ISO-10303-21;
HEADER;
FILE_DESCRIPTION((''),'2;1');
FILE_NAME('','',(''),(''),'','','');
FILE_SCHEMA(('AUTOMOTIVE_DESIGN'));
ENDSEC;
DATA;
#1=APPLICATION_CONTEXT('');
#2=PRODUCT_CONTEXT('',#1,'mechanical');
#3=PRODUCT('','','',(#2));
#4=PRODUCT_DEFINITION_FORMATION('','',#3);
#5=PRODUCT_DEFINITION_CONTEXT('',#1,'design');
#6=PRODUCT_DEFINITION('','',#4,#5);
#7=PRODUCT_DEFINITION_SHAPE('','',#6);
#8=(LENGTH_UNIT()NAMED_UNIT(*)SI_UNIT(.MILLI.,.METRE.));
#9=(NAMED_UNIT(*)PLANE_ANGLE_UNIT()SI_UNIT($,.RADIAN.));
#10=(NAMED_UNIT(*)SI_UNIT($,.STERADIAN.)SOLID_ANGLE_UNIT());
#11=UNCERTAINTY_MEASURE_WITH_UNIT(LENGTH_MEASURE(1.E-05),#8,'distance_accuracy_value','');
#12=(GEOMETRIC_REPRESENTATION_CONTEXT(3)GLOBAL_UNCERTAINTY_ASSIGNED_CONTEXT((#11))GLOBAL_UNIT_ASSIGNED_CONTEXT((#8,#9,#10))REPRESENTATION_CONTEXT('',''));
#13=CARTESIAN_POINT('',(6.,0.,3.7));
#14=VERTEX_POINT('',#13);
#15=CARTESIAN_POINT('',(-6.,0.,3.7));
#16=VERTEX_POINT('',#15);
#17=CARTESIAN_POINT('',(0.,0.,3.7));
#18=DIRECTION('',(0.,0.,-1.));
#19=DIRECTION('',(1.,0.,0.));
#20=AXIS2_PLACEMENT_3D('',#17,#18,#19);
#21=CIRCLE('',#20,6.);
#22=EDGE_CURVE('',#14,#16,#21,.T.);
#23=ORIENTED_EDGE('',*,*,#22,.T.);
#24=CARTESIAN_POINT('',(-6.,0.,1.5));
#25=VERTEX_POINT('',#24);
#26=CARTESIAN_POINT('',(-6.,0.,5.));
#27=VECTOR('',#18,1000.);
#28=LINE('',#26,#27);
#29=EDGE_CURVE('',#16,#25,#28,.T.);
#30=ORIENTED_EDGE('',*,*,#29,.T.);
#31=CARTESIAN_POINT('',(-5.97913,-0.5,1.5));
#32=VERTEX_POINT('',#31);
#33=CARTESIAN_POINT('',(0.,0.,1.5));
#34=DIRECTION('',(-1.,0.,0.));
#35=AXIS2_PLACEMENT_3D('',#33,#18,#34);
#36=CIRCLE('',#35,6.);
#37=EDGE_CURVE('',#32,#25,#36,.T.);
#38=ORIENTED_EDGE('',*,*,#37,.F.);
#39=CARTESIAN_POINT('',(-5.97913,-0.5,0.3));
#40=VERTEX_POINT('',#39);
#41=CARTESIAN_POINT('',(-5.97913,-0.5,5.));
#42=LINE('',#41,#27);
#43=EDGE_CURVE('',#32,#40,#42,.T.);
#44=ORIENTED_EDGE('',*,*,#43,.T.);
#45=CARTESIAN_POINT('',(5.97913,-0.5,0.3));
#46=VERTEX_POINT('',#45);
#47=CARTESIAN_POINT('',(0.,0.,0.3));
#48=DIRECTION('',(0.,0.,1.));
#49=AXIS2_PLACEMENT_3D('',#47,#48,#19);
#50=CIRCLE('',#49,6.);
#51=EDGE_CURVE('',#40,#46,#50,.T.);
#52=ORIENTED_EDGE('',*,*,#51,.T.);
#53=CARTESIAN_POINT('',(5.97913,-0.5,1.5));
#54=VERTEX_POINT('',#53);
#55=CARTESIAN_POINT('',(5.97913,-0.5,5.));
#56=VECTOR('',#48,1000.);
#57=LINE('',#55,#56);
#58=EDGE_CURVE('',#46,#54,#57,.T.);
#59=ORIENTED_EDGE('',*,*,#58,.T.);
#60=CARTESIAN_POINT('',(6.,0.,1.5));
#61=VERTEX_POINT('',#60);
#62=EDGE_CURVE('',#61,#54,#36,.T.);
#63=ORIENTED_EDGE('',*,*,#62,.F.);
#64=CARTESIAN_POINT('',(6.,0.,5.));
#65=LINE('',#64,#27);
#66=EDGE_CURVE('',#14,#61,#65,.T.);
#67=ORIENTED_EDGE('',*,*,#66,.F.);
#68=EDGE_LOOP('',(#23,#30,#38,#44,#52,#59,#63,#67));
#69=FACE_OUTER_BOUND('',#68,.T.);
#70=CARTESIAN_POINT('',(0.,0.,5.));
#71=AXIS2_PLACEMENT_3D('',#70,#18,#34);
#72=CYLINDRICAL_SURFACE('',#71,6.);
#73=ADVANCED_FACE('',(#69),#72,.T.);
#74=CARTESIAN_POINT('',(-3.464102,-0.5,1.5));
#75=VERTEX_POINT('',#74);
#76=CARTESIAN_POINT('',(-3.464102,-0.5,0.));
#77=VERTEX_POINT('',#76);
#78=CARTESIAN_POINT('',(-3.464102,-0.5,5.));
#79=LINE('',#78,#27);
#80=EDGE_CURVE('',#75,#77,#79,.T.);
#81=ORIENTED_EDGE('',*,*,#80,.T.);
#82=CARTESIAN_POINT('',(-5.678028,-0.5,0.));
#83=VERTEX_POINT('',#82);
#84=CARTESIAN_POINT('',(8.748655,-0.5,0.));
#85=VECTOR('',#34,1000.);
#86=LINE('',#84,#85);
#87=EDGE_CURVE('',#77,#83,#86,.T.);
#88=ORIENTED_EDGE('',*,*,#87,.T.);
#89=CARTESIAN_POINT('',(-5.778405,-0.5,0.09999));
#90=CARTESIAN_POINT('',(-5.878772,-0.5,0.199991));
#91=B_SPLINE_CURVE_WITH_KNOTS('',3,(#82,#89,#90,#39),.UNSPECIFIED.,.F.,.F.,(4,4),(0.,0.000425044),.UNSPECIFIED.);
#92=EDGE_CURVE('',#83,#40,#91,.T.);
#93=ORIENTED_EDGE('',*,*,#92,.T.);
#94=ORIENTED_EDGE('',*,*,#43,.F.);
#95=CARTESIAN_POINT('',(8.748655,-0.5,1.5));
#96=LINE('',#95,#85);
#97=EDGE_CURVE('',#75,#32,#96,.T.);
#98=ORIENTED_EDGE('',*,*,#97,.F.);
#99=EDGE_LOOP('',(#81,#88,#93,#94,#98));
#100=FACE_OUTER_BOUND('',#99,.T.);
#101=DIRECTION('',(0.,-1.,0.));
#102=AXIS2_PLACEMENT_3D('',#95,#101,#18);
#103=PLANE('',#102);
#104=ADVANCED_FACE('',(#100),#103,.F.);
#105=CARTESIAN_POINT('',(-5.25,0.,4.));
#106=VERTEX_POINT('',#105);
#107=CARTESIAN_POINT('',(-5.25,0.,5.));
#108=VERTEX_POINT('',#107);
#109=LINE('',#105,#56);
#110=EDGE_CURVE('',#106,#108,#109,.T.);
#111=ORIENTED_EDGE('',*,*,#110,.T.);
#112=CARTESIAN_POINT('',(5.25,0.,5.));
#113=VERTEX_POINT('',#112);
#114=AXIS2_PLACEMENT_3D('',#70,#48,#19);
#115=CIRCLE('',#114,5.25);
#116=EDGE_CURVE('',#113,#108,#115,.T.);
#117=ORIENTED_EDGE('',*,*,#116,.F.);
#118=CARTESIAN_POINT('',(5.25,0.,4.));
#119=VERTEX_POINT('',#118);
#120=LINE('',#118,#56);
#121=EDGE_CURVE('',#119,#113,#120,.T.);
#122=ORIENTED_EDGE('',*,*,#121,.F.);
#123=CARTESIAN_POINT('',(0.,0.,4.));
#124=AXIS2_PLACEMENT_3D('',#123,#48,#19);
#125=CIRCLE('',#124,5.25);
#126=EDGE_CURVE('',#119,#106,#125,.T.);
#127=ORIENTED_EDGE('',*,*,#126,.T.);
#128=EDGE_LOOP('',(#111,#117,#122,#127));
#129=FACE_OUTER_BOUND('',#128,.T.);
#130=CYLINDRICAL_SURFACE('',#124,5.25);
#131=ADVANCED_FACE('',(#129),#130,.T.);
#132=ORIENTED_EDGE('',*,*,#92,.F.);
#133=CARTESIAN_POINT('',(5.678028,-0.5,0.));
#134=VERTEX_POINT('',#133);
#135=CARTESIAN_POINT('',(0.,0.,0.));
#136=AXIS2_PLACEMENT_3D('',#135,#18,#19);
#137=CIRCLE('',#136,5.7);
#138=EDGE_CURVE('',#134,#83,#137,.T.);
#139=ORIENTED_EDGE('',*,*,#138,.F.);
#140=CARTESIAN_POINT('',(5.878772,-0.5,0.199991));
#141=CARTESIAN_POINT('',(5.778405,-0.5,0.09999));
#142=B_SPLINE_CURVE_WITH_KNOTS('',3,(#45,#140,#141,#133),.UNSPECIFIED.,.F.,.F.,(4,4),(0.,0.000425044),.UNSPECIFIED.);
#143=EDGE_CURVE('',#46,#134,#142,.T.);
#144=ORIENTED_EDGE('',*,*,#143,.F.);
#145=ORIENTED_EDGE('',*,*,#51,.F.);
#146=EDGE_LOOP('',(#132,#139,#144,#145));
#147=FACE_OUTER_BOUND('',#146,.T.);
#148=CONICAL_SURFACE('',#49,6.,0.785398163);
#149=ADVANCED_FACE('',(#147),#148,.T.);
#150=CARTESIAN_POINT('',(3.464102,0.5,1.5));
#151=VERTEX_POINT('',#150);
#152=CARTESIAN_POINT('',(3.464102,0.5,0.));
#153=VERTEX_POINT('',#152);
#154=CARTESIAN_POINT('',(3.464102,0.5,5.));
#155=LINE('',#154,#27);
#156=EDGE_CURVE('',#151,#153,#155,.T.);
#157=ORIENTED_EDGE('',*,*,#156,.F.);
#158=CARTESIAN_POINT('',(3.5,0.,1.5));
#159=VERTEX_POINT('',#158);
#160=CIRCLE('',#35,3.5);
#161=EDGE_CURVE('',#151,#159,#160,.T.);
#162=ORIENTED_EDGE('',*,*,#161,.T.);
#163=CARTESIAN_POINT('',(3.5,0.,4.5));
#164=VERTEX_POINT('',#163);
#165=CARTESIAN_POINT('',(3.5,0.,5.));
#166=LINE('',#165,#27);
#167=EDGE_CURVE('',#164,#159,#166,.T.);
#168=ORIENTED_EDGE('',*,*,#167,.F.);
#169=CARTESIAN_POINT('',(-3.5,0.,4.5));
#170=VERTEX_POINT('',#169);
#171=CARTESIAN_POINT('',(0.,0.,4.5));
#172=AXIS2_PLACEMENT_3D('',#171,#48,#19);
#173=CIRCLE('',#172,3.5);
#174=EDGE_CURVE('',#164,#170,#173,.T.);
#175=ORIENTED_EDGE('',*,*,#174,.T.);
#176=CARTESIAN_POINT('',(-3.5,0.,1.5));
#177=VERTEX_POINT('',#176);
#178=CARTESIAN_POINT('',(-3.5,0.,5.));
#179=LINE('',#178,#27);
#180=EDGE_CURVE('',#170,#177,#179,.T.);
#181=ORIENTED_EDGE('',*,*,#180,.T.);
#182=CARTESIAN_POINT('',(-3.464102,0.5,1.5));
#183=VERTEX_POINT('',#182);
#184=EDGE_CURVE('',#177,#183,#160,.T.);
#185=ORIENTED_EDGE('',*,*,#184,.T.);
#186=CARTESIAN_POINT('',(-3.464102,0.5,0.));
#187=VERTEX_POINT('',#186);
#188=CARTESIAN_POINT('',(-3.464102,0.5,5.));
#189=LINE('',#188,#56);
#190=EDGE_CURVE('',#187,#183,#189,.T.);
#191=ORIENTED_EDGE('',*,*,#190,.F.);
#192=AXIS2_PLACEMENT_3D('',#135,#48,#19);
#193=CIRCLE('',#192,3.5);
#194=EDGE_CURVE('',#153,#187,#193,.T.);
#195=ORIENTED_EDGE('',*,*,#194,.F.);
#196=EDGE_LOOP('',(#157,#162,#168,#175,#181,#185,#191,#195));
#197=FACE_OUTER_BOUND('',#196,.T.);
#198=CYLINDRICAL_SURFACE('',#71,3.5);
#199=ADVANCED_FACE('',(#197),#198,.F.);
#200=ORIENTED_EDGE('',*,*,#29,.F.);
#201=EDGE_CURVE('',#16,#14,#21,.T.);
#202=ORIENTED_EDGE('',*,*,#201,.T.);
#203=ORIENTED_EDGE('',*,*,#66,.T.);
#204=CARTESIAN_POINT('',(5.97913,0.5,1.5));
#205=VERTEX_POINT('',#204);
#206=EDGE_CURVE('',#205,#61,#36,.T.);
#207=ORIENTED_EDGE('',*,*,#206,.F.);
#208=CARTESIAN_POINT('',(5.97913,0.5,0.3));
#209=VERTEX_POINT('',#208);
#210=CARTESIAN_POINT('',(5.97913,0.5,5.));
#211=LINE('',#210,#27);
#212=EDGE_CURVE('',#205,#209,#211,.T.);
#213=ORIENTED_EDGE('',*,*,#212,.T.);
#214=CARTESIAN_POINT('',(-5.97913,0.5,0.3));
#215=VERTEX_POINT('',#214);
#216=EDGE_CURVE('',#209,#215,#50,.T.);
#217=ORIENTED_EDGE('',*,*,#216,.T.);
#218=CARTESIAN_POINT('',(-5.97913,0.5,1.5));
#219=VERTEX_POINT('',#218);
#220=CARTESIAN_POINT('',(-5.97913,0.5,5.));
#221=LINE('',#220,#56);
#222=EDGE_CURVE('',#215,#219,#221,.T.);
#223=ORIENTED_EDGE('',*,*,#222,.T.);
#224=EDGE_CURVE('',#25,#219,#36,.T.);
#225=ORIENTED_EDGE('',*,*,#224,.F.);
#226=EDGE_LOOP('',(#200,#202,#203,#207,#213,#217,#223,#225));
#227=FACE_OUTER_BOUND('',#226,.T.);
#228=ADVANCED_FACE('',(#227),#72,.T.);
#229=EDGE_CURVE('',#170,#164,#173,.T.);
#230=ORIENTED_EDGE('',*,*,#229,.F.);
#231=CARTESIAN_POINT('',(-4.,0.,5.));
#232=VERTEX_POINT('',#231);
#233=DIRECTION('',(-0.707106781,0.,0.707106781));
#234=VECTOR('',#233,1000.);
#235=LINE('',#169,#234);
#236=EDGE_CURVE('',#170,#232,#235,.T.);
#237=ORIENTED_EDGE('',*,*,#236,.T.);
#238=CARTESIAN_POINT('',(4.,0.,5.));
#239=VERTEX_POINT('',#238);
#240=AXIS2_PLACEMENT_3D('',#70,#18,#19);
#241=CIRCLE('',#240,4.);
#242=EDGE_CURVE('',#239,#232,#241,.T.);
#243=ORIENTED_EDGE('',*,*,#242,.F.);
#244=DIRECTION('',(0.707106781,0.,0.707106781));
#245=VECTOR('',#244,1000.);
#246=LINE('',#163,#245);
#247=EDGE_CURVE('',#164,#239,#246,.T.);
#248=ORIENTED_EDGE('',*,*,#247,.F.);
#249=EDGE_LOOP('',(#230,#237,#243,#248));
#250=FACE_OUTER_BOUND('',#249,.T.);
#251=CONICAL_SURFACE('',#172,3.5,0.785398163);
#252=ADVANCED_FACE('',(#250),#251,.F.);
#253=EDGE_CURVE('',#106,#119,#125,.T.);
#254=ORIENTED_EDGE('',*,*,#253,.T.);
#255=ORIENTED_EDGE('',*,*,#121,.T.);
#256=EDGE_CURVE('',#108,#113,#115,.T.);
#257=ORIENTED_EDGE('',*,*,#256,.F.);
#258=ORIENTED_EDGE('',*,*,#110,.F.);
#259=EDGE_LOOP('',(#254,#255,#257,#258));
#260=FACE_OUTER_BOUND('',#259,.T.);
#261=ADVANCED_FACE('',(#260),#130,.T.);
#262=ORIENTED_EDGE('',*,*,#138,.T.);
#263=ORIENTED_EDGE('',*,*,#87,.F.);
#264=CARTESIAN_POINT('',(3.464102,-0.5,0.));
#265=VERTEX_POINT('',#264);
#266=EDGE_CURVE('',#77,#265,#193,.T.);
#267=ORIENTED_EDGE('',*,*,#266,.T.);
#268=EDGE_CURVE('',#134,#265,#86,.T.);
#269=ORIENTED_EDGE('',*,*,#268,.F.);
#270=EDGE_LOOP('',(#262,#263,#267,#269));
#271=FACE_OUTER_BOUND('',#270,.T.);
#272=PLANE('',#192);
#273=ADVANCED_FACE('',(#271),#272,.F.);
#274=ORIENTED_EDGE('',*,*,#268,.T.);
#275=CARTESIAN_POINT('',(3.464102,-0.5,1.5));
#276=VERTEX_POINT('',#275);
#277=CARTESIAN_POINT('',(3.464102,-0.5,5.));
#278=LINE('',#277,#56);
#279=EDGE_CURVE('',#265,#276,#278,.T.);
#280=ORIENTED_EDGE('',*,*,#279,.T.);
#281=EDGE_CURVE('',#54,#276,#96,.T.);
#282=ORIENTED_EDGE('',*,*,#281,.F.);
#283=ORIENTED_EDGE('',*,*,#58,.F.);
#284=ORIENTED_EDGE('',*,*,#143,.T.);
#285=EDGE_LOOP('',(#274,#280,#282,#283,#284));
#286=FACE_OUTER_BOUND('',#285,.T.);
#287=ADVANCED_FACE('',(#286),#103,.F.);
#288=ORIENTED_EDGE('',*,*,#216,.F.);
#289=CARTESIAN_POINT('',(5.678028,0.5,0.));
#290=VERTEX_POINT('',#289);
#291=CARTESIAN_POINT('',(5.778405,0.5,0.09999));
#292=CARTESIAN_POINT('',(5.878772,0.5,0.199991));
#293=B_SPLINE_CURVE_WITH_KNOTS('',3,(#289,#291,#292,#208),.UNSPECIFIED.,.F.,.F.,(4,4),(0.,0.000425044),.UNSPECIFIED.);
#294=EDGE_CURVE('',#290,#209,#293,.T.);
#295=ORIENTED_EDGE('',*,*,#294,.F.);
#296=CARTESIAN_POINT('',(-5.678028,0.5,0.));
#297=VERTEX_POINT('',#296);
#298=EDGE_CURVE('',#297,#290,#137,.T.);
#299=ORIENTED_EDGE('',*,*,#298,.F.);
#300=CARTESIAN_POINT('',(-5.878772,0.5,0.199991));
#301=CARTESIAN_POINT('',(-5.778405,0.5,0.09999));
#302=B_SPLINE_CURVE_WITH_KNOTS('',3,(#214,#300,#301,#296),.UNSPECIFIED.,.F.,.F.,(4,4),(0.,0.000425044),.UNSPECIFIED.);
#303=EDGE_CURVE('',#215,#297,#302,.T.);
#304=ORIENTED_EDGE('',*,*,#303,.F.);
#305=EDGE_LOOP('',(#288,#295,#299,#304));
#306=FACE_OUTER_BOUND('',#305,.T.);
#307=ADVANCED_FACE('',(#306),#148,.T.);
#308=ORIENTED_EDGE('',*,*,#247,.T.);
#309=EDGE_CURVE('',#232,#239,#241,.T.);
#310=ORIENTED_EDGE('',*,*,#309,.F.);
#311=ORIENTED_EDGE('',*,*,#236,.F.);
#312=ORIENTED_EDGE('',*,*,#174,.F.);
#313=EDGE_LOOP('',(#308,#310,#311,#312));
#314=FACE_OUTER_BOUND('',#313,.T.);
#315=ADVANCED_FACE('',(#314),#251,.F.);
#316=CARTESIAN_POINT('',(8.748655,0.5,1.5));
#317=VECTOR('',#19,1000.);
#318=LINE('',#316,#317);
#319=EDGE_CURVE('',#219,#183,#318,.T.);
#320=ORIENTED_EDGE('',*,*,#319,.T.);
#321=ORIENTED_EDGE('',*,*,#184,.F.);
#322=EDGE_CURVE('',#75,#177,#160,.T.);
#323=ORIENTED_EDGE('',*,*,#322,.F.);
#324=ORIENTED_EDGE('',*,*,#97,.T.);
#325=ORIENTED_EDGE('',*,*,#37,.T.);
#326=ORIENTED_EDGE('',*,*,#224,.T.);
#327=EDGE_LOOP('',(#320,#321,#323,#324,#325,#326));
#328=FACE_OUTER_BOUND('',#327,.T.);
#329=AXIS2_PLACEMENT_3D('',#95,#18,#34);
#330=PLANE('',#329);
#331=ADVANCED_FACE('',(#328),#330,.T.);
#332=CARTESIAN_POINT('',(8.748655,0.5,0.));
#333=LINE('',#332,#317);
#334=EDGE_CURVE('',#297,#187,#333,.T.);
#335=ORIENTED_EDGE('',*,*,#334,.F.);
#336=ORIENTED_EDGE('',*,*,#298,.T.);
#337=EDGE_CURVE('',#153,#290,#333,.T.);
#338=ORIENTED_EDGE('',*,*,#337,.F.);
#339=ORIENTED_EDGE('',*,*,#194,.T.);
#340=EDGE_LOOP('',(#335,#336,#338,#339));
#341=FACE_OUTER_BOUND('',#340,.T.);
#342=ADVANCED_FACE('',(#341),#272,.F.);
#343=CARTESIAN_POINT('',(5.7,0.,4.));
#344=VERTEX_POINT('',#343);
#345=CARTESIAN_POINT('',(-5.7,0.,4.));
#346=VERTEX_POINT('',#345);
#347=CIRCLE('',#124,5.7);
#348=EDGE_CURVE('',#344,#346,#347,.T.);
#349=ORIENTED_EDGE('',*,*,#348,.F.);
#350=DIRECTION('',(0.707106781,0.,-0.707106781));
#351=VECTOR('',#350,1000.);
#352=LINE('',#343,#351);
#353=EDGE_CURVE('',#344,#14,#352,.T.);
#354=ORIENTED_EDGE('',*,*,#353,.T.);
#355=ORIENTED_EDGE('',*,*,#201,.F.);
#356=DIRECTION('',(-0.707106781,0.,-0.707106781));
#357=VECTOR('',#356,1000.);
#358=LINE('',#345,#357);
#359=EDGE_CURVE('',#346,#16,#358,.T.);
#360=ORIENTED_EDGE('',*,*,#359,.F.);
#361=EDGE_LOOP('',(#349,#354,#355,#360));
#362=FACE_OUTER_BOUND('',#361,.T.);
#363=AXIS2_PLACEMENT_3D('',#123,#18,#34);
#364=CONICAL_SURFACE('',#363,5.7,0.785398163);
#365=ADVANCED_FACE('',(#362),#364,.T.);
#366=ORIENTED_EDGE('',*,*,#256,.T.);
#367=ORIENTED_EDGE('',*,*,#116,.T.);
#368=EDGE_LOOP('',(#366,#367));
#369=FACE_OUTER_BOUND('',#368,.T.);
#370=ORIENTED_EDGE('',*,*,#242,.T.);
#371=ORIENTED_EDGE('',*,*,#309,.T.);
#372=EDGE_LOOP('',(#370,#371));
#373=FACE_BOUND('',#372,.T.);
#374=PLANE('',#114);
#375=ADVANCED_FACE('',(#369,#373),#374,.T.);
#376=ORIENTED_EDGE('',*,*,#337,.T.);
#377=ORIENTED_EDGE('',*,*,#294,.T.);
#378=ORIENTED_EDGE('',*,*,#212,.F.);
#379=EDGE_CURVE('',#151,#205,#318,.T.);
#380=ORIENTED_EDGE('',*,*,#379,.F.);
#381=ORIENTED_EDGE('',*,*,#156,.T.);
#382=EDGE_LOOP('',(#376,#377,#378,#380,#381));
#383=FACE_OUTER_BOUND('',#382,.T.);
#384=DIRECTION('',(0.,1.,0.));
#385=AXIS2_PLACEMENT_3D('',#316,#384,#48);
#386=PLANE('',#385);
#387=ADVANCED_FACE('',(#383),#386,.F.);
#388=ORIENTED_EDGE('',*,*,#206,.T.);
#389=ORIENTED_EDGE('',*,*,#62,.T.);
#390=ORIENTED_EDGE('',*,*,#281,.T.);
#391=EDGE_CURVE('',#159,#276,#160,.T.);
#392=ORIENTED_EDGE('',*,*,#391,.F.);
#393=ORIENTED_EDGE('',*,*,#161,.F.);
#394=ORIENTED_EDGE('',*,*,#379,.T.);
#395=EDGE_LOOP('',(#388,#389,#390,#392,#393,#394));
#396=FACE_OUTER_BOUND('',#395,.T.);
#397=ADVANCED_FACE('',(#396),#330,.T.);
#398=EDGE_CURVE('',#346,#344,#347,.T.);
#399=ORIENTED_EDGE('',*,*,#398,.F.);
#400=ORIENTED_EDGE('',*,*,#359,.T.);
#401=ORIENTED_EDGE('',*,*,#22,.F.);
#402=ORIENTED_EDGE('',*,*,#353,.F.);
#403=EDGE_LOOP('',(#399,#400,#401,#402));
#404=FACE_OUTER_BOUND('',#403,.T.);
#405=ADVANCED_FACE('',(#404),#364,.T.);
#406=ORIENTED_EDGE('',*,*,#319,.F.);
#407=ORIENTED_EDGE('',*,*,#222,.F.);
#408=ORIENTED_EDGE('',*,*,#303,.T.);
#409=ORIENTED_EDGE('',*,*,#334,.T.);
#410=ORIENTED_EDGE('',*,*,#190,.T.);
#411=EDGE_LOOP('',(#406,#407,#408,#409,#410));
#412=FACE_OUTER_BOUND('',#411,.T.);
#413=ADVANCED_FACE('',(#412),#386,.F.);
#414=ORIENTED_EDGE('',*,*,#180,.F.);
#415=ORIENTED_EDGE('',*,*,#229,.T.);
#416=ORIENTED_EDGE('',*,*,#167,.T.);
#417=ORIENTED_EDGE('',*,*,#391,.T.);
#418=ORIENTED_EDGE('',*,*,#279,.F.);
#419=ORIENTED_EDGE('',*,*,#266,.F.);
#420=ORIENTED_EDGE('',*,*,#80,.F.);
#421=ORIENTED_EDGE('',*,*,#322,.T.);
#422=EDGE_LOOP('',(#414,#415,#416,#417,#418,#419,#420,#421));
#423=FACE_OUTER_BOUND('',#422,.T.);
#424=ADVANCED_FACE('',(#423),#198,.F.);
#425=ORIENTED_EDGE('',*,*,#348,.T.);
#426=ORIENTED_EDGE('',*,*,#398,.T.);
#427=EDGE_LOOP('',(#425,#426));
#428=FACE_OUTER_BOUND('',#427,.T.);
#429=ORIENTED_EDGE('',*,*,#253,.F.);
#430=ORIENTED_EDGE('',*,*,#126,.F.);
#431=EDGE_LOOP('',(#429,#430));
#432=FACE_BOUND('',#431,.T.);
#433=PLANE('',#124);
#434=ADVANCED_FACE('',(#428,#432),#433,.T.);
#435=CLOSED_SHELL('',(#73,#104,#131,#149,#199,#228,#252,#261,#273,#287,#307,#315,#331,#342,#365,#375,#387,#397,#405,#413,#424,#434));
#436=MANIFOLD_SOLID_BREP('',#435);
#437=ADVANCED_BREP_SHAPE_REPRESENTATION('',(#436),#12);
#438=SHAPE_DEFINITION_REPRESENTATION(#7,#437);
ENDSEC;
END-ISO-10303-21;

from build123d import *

# Parameters (mm, degrees)
SKETCH_1_R          = 6
SKETCH_1_R_2        = 3.5
EXTRUDE_1_DEPTH     = 5
CHAMFER_1_SIZE      = 0.5
SKETCH_2_W          = 16.841160442
SKETCH_2_H          = 1
CUT_EXTRUDE_1_DEPTH = 1.5
CUT_EXTRUDE_START   = -1
SKETCH_3_R          = 6
SKETCH_3_R_2        = 5.25
CUT_EXTRUDE_2_DEPTH = 1
CHAMFER_2_SIZE      = 0.3


with BuildPart() as part:
    # 草图1 → 凸台-拉伸1 (new body)
    with BuildSketch(Plane.XY):
        Circle(SKETCH_1_R)
        Circle(SKETCH_1_R_2, mode=Mode.SUBTRACT)
    extrude(amount=EXTRUDE_1_DEPTH)

    # 倒角1
    chamfer_1_edges = [part.edges().sort_by_distance(p)[0] for p in [
        (-3.5, 0, 5),
    ]]
    chamfer(chamfer_1_edges, length=CHAMFER_1_SIZE)

    # 草图2 → 切除-拉伸1 (cut)
    with BuildSketch(Plane(origin=(0, 0, 0), x_dir=(-1, 0, 0), z_dir=(0, 0, -1))):
        with Locations((-0.328074554, 0)):
            Rectangle(SKETCH_2_W, SKETCH_2_H)
    extrude(amount=-CUT_EXTRUDE_1_DEPTH, mode=Mode.SUBTRACT)

    # 草图3 → 切除-拉伸2 (cut)
    with BuildSketch(Plane.XY.offset(5).offset(CUT_EXTRUDE_START)):
        with Locations(Location((0, 0, 0), (0, 0, 175.219808153))):
            Circle(SKETCH_3_R)
        Circle(SKETCH_3_R_2, mode=Mode.SUBTRACT)
    extrude(amount=CUT_EXTRUDE_2_DEPTH, mode=Mode.SUBTRACT)

    # 倒角2
    chamfer_2_edges = [part.edges().sort_by_distance(p)[0] for p in [
        (0, -6, 0),
        (0, 6, 0),
        (-6, 0, 4),
    ]]
    chamfer(chamfer_2_edges, length=CHAMFER_2_SIZE)


solid = part.part
